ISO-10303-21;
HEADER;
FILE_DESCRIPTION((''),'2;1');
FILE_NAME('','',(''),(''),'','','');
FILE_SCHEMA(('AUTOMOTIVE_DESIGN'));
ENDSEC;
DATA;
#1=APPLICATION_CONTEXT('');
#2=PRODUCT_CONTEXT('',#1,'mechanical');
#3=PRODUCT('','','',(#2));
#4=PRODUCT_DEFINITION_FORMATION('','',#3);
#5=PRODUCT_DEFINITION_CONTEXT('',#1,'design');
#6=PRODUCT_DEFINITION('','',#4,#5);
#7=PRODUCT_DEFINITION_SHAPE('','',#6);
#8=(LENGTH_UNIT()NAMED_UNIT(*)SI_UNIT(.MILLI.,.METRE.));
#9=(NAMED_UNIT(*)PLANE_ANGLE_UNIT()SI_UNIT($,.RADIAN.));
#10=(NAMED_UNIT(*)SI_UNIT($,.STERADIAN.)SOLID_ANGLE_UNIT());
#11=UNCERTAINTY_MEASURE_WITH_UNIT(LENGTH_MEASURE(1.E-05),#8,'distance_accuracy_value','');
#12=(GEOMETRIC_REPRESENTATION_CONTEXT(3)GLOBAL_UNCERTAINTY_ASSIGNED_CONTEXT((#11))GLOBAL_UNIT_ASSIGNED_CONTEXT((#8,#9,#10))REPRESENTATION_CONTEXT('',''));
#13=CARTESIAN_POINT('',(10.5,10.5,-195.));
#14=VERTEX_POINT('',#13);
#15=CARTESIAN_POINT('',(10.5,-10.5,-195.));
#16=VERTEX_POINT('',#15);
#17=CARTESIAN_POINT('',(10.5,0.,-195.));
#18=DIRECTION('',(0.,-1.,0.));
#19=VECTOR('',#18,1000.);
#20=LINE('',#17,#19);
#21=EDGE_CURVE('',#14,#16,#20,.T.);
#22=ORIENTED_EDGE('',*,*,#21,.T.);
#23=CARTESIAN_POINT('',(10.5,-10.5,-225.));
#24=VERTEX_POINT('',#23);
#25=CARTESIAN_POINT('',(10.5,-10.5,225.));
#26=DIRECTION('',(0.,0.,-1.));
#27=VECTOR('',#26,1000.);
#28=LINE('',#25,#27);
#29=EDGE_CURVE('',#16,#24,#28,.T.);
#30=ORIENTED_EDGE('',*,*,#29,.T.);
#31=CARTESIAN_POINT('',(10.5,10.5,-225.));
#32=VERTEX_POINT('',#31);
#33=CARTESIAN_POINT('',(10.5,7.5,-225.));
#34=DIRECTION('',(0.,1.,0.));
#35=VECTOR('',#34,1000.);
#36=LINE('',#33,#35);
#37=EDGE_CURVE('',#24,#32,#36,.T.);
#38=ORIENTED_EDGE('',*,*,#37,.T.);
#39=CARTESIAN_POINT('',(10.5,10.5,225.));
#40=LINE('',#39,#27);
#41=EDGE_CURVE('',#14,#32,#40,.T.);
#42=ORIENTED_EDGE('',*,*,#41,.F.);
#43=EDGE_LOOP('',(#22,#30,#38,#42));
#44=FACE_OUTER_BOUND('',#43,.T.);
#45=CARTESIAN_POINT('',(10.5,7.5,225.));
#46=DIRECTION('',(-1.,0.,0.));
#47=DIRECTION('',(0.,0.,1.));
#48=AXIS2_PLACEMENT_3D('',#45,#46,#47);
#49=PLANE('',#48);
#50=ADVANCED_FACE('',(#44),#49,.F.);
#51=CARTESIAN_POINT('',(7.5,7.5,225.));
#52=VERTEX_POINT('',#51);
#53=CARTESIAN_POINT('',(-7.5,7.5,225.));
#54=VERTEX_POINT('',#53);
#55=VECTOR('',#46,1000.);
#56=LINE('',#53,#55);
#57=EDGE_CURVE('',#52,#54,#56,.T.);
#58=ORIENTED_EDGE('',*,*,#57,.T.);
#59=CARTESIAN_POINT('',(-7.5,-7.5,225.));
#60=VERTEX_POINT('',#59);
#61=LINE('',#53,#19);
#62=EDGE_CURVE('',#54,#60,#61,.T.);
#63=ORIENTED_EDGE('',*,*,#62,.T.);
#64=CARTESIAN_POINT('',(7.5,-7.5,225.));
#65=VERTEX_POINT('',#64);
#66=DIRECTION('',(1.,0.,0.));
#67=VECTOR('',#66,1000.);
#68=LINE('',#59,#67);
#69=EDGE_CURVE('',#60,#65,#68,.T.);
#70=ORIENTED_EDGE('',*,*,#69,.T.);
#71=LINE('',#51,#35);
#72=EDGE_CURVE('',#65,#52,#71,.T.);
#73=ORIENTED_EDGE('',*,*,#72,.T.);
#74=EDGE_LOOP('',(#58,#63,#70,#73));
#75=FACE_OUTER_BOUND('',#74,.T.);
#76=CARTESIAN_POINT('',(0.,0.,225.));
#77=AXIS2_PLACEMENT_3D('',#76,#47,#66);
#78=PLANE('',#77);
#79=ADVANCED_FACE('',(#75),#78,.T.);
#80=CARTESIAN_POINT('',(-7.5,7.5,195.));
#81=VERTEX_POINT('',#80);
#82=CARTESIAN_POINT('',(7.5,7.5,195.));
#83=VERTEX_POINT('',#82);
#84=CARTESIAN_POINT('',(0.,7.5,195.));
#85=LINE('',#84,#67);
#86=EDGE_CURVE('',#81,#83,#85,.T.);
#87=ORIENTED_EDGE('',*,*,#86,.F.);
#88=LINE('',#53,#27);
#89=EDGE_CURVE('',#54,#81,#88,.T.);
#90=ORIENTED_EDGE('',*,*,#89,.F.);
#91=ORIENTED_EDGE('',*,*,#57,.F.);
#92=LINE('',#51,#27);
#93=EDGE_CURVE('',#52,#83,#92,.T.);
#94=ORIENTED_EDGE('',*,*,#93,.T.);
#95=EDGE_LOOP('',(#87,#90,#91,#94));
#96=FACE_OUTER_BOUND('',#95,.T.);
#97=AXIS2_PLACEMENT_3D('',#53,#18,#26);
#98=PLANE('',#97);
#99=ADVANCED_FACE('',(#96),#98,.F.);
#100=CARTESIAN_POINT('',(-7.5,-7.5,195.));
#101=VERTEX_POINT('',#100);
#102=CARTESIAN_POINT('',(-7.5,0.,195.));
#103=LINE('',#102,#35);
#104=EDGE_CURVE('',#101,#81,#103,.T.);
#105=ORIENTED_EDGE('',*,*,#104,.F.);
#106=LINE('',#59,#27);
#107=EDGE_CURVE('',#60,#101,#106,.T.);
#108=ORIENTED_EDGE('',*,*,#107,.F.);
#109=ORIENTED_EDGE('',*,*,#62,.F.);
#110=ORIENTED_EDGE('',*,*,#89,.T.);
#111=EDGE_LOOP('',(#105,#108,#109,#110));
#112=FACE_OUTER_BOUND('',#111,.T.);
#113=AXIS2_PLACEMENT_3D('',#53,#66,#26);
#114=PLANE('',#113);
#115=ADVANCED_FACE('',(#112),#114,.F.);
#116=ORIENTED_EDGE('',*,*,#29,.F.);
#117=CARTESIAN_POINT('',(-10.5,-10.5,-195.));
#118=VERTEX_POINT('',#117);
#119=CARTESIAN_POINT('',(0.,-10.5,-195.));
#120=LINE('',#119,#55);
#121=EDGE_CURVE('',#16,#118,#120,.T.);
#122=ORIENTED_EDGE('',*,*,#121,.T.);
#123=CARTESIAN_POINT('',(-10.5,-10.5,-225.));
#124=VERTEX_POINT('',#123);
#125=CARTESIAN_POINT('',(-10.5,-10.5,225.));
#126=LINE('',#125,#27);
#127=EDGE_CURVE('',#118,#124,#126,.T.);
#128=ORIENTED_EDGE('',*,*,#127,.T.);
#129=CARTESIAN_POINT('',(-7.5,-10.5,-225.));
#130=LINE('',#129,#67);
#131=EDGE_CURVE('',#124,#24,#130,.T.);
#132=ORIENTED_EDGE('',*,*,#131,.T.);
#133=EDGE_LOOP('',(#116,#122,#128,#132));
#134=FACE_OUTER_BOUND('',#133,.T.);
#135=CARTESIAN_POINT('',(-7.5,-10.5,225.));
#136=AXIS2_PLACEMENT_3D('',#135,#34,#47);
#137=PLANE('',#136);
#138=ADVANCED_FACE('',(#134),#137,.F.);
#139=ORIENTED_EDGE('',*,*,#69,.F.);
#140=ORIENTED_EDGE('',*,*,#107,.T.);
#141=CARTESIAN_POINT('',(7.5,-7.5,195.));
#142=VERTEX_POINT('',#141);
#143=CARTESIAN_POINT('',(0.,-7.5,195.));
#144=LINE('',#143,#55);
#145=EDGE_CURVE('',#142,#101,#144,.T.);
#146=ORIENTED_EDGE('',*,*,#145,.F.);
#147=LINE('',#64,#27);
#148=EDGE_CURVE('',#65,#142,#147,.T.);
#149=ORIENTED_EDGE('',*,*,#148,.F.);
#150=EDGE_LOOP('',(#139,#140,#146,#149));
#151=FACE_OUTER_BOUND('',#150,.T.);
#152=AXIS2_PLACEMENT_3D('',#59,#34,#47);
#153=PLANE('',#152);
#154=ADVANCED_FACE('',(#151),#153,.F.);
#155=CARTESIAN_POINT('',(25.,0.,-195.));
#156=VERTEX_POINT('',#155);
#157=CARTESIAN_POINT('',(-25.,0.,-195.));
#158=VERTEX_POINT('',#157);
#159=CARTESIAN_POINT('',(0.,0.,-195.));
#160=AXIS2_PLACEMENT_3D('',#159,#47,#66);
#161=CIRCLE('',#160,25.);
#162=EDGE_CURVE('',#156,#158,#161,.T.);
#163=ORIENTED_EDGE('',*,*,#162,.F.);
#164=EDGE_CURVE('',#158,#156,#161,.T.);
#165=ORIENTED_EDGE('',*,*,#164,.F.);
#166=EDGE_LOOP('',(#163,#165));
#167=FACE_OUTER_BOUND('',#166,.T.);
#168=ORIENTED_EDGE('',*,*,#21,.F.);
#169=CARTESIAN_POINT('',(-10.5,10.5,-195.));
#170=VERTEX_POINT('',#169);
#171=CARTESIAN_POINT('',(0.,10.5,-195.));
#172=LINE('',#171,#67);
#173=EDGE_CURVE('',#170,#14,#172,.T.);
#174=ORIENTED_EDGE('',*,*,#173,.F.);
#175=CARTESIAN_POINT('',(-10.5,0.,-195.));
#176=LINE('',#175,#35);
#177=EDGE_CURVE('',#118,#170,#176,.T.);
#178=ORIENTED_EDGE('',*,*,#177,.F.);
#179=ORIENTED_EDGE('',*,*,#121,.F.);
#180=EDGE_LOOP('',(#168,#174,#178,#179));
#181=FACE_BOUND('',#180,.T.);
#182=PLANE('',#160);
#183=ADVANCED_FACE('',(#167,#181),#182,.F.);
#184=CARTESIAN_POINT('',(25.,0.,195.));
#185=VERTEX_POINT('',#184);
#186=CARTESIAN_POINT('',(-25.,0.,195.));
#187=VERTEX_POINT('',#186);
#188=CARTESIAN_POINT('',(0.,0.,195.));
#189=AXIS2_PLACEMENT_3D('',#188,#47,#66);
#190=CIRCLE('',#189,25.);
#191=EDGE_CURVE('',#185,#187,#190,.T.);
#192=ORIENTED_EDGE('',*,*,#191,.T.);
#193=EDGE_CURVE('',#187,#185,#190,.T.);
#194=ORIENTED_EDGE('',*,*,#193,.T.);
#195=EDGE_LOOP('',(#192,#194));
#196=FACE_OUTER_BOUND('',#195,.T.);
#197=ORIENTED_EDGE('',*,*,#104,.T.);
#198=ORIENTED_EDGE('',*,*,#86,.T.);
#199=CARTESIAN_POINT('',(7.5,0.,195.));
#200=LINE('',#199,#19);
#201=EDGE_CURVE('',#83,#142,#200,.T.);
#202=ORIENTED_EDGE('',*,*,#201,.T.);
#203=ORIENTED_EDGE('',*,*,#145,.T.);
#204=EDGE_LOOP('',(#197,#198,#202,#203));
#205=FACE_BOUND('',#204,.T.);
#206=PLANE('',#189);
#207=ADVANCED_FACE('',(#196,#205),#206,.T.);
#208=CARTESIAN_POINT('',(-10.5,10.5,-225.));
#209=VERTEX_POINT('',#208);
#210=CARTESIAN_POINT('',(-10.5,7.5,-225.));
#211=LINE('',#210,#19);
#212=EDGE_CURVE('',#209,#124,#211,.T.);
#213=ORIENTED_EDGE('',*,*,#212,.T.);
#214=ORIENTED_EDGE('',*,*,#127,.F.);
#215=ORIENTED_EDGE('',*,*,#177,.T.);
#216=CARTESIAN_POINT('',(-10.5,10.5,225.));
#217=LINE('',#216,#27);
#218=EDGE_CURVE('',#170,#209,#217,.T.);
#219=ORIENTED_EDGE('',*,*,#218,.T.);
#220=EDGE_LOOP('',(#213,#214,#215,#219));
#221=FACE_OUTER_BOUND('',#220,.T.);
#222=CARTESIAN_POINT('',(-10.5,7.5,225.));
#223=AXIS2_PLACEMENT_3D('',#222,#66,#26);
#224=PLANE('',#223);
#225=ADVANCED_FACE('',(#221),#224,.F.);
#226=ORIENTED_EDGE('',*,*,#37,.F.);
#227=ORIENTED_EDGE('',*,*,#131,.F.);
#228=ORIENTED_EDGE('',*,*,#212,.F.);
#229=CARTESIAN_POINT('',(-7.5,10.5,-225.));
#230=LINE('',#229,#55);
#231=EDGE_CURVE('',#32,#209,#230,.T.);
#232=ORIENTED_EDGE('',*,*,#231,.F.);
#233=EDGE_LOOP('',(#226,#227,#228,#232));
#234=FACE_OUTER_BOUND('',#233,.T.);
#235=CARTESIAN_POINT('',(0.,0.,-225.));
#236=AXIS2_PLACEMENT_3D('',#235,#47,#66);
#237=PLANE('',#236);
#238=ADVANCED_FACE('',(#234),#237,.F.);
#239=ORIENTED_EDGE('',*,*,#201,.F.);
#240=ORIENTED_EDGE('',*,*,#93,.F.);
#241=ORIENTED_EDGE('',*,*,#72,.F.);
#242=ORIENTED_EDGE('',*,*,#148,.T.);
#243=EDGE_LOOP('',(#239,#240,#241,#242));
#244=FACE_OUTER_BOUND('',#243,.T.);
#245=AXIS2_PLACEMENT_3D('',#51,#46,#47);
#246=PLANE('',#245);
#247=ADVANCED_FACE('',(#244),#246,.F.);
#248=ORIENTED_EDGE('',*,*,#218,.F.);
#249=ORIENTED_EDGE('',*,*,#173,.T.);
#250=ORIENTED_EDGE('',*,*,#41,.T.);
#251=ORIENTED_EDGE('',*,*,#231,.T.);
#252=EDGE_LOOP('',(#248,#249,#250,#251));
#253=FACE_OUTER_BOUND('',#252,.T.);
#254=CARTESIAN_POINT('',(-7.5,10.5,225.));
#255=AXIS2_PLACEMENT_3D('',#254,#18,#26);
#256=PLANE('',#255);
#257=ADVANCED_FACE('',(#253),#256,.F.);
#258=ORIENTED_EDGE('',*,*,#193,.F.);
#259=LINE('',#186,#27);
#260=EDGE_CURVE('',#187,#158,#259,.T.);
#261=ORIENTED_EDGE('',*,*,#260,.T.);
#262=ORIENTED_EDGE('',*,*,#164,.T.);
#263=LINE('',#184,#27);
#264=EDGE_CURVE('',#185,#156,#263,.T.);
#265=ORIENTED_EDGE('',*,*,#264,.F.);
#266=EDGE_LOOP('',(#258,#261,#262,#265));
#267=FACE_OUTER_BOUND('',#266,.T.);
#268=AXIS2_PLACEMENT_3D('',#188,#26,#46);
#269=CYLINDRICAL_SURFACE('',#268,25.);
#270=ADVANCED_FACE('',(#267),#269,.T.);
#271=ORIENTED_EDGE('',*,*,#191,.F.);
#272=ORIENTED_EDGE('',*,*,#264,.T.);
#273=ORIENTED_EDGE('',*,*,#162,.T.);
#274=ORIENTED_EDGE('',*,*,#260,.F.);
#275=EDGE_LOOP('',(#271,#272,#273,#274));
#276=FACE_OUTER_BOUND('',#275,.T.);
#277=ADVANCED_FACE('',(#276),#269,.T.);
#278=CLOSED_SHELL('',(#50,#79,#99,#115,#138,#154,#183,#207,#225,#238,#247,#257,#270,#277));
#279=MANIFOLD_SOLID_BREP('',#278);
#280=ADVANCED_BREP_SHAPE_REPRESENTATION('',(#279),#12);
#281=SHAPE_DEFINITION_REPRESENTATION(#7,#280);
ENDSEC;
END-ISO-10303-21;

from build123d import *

# Parameters (mm, degrees)
SKETCH_1_R       = 25
EXTRUDE_1_DEPTH  = 195
SKETCH_2_W       = 15
SKETCH_2_H       = 15
EXTRUDE_2_DEPTH  = 225
MOVE_FACE_1_BY   = 3
MOVE_FACE_1_2_BY = 3
MOVE_FACE_1_3_BY = 3
MOVE_FACE_1_4_BY = 3


with BuildPart() as part:
    # 草图1 → 凸台-拉伸1 (new, symmetric)
    with BuildSketch(Plane.XY):
        Circle(SKETCH_1_R)
    extrude(amount=EXTRUDE_1_DEPTH, both=True)

    # 草图2 → 凸台-拉伸2 (add, symmetric)
    with BuildSketch(Plane.XY):
        Rectangle(SKETCH_2_W, SKETCH_2_H)
    extrude(amount=EXTRUDE_2_DEPTH, both=True)

    # Move Face 1: a face moved outward by 3.0
    extrude(part.faces().sort_by_distance((7.5, 0, -210))[0], amount=MOVE_FACE_1_BY, dir=(1, 0, 0))

    # Move Face 1 2: a face moved outward by 3.0
    extrude(part.faces().sort_by_distance((0, -7.5, -210))[0], amount=MOVE_FACE_1_2_BY, dir=(0, -1, 0))

    # Move Face 1 3: a face moved outward by 3.0
    extrude(part.faces().sort_by_distance((-7.5, 0, -210))[0], amount=MOVE_FACE_1_3_BY, dir=(-1, 0, 0))

    # Move Face 1 4: a face moved outward by 3.0
    extrude(part.faces().sort_by_distance((0, 7.5, -210))[0], amount=MOVE_FACE_1_4_BY, dir=(0, 1, 0))


solid = part.part
